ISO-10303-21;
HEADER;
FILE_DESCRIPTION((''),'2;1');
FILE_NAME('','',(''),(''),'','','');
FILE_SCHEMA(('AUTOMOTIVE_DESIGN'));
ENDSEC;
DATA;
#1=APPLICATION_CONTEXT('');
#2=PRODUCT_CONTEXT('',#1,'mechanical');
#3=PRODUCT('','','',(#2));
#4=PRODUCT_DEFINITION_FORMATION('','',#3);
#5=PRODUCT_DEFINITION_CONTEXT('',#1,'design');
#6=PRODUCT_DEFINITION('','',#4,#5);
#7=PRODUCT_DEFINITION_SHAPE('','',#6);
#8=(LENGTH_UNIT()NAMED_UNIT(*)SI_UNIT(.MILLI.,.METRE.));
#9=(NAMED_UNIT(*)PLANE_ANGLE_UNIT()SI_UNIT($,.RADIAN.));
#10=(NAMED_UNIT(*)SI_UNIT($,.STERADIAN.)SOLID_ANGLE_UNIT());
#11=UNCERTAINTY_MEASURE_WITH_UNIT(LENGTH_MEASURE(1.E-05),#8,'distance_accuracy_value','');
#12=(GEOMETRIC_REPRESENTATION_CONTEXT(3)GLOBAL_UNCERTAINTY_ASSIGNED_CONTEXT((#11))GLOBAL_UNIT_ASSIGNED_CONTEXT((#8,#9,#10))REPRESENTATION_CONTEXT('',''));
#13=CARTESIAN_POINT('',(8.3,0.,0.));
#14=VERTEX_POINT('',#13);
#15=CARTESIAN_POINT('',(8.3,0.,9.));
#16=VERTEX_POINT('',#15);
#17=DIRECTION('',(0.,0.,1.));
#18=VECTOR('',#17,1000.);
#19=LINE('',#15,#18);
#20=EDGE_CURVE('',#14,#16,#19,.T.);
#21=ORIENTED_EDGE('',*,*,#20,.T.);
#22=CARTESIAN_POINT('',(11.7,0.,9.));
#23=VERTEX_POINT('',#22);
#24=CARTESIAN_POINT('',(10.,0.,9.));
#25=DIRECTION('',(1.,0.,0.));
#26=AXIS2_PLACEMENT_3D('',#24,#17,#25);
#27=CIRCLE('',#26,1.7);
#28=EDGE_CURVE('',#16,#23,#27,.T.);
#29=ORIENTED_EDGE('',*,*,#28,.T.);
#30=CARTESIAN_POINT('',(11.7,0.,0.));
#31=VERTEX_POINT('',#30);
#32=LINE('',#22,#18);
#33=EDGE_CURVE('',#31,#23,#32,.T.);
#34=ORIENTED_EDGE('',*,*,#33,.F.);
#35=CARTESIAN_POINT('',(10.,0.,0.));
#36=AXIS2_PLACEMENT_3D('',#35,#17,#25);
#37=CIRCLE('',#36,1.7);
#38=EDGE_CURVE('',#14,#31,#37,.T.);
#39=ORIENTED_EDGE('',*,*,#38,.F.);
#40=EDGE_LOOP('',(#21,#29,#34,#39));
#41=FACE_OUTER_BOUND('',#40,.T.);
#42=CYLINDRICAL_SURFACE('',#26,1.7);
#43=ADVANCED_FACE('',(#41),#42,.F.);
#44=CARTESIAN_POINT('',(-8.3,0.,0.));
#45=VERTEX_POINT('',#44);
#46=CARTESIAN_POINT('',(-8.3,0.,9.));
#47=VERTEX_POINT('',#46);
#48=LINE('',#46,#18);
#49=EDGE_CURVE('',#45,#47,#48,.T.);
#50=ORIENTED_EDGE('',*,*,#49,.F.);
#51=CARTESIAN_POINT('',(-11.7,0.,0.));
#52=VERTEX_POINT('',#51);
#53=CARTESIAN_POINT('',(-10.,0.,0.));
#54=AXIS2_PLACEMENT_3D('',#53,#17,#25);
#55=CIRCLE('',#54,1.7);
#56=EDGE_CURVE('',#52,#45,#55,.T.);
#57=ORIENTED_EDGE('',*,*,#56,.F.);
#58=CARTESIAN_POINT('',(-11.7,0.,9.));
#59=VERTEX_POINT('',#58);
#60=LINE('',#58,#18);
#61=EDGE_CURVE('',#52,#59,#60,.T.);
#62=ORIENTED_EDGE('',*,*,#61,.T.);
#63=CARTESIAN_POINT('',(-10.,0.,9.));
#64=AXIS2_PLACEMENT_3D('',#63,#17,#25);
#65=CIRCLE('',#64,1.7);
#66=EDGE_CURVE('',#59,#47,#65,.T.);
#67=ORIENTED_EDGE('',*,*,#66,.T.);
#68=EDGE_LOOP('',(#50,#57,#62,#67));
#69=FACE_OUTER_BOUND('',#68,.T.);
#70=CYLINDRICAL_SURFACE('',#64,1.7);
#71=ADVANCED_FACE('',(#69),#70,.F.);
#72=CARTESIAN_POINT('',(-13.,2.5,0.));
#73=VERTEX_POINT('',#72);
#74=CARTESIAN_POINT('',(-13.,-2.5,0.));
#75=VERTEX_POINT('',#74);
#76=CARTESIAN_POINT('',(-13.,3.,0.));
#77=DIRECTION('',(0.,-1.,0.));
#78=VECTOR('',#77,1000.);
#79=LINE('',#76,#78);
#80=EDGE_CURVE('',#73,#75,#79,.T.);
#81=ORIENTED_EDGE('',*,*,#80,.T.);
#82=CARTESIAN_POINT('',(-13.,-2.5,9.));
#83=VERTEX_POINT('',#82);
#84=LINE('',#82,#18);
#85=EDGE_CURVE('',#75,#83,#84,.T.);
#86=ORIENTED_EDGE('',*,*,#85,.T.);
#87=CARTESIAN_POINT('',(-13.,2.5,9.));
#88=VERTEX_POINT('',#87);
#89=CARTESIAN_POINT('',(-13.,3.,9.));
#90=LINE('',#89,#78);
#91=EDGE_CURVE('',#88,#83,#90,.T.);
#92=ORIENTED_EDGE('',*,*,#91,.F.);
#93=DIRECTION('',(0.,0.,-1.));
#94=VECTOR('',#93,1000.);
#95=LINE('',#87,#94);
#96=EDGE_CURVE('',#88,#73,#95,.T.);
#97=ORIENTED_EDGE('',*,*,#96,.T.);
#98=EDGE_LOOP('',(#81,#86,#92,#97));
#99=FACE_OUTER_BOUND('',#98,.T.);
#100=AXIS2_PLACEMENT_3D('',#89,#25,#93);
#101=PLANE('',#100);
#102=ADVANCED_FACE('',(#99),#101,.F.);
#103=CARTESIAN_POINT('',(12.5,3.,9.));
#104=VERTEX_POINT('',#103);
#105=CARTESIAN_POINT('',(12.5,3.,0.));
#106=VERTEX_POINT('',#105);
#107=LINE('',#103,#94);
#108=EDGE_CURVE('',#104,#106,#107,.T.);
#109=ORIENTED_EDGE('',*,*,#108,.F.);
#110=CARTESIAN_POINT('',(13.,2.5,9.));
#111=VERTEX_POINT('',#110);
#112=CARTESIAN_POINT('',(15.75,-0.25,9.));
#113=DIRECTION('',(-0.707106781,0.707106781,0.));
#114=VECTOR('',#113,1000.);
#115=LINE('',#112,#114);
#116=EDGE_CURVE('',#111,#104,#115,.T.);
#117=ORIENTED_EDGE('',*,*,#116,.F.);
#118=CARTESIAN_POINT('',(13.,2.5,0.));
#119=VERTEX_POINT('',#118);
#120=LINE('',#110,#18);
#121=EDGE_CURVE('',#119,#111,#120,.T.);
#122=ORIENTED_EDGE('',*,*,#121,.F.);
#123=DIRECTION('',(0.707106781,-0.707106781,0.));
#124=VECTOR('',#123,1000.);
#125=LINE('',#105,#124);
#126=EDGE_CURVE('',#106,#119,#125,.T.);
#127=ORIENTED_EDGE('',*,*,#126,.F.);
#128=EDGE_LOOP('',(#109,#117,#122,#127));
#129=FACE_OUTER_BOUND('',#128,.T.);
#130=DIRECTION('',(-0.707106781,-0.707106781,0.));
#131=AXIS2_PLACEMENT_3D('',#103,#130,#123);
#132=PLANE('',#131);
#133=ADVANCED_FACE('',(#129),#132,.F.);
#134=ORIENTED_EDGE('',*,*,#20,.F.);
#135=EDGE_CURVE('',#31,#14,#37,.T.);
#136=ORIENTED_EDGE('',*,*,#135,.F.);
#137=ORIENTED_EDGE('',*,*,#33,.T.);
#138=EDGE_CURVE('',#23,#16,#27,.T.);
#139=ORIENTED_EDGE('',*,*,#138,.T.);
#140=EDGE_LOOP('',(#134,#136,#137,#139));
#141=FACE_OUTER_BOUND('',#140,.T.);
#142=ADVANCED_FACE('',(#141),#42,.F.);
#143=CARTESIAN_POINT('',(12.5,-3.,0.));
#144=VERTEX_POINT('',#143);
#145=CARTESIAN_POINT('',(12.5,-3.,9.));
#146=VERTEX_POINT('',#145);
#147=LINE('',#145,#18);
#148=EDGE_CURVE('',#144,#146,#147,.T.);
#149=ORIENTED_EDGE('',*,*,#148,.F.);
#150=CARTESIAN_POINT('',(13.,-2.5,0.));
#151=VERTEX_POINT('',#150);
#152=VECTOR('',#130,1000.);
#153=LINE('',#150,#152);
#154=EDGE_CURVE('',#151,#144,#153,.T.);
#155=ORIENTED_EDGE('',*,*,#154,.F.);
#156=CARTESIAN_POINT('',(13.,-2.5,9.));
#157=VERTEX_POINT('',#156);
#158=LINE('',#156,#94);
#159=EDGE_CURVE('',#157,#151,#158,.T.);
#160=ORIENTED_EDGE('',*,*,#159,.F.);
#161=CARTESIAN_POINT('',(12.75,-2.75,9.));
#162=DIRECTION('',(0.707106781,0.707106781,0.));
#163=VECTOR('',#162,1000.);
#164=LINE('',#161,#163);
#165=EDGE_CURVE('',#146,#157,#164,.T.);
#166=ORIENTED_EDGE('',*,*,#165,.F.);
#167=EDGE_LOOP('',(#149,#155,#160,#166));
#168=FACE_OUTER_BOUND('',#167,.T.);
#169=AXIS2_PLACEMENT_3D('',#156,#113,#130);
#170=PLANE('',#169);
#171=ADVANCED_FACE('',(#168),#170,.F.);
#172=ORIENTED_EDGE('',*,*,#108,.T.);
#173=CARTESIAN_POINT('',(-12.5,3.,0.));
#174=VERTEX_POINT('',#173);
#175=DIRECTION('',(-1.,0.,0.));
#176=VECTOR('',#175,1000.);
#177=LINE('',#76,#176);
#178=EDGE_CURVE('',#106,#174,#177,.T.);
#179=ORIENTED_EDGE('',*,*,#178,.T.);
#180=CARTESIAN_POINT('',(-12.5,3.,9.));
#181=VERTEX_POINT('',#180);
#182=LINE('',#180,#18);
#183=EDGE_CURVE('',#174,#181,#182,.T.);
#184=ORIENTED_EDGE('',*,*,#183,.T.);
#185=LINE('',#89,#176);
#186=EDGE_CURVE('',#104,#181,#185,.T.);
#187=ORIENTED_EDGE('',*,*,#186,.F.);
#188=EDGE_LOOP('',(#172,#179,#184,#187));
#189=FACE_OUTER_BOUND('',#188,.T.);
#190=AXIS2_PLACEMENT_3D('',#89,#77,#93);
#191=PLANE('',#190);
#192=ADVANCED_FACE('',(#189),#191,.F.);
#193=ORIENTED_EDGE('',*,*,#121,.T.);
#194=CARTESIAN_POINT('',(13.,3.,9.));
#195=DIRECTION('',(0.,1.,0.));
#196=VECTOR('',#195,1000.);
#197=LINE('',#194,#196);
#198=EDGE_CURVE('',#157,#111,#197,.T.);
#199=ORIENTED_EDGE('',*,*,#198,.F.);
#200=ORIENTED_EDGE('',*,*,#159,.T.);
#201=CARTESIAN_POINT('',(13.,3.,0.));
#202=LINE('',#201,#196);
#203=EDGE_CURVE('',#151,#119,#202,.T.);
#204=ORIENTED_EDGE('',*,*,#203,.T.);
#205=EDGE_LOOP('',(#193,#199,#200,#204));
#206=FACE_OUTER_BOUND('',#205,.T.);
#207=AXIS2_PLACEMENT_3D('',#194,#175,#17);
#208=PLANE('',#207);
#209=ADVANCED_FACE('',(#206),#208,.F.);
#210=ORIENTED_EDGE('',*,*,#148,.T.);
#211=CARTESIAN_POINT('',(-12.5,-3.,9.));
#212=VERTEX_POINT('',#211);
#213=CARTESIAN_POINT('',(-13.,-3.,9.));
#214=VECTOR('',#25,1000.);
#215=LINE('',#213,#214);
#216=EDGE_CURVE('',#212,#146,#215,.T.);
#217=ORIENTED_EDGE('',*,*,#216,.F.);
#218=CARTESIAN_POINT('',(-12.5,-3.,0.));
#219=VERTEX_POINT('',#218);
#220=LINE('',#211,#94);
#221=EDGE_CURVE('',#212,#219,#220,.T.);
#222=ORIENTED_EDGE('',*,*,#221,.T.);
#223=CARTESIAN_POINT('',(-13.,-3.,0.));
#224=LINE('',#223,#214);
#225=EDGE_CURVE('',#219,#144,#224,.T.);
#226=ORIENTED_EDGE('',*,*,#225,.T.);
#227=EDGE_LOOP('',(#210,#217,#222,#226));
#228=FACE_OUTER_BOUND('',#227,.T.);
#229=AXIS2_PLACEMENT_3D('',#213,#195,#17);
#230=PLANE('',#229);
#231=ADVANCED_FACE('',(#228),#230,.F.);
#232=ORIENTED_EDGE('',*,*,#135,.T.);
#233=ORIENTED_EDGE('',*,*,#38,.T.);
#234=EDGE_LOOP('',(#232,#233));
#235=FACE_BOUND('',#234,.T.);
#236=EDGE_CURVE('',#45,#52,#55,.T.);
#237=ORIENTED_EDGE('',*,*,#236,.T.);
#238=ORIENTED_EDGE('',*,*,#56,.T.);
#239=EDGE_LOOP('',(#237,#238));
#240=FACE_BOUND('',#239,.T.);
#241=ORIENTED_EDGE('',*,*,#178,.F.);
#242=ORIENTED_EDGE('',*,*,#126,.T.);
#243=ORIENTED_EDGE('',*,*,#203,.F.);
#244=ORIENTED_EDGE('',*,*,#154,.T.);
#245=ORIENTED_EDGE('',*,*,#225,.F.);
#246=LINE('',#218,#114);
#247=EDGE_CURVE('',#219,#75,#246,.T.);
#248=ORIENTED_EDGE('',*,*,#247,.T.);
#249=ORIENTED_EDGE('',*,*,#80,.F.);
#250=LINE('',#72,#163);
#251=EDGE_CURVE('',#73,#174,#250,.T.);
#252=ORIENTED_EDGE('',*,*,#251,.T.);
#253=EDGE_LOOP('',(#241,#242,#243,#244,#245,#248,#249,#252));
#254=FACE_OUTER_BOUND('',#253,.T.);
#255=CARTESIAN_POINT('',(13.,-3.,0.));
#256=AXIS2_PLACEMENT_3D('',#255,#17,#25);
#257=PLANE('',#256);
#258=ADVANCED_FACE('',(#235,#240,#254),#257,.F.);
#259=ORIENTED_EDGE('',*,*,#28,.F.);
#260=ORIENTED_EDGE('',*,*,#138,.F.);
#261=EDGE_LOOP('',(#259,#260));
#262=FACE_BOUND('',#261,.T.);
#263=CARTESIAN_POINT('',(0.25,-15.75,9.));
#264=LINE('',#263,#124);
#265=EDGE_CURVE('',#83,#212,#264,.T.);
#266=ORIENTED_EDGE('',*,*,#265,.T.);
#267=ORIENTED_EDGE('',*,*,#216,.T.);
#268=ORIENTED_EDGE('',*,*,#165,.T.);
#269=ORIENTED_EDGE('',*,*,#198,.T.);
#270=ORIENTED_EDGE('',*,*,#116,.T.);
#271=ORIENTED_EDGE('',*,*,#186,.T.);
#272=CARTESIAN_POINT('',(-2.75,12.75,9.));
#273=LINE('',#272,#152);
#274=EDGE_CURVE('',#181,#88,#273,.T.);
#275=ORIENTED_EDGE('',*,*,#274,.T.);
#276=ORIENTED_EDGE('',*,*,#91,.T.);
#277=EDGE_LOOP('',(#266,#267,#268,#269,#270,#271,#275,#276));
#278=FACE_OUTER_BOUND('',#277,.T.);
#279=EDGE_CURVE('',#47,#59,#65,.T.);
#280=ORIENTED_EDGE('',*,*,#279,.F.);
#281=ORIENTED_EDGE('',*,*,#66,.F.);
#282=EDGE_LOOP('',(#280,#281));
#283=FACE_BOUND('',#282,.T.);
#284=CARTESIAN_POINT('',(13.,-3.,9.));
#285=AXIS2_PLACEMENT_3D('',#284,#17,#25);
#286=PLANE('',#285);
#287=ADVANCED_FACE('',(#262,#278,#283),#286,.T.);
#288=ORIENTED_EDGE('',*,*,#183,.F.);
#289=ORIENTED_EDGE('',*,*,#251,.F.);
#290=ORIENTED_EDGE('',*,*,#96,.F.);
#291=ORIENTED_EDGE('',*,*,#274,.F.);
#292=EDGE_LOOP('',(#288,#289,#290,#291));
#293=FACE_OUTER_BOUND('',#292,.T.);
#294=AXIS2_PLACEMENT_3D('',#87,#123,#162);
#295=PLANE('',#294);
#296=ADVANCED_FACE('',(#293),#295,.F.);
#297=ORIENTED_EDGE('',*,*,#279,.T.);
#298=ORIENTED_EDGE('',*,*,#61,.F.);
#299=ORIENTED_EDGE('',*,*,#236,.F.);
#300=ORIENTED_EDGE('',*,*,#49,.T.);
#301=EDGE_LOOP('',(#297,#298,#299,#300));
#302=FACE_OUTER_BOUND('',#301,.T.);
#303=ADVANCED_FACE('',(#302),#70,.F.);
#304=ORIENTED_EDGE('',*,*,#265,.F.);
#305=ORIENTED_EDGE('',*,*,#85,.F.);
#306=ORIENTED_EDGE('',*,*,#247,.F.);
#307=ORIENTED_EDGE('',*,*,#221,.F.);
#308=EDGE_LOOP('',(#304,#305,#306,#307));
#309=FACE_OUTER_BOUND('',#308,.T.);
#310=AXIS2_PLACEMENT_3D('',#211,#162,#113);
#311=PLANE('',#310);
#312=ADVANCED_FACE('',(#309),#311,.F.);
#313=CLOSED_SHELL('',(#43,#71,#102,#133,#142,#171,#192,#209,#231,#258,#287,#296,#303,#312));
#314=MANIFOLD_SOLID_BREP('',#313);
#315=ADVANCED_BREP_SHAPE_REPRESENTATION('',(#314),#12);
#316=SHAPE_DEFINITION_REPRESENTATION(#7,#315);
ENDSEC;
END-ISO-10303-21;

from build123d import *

# Parameters (mm, degrees)
SKETCH1_W                = 26
SKETCH1_H                = 6
BOSS_EXTRUDE1_DEPTH      = 9
M3_CLEARANCE_HOLE1_D     = 3.4
M3_CLEARANCE_HOLE1_DEPTH = 30
M3_CLEARANCE_HOLE1_TIP   = 1.021463052
CHAMFER1_SIZE            = 0.5


with BuildPart() as part:
    # Sketch1 → Boss-Extrude1 (new body)
    with BuildSketch(Plane.XY):
        Rectangle(SKETCH1_W, SKETCH1_H)
    extrude(amount=BOSS_EXTRUDE1_DEPTH)

    # M3 Clearance Hole1
    with Locations(Plane.XY.offset(9)):
        with Locations((-10, 0), (10, 0)):
            Hole(M3_CLEARANCE_HOLE1_D / 2, depth=M3_CLEARANCE_HOLE1_DEPTH)
            with Locations((0, 0, -(M3_CLEARANCE_HOLE1_DEPTH + M3_CLEARANCE_HOLE1_TIP / 2))):  # 118° drill point
                Cone(0, M3_CLEARANCE_HOLE1_D / 2, M3_CLEARANCE_HOLE1_TIP, mode=Mode.SUBTRACT)

    # Chamfer1
    chamfer1_edges = [part.edges().sort_by_distance(p)[0] for p in [
        (13, -3, 4.5),
        (-13, -3, 4.5),
        (-13, 3, 4.5),
        (13, 3, 4.5),
    ]]
    chamfer(chamfer1_edges, length=CHAMFER1_SIZE)


solid = part.part
